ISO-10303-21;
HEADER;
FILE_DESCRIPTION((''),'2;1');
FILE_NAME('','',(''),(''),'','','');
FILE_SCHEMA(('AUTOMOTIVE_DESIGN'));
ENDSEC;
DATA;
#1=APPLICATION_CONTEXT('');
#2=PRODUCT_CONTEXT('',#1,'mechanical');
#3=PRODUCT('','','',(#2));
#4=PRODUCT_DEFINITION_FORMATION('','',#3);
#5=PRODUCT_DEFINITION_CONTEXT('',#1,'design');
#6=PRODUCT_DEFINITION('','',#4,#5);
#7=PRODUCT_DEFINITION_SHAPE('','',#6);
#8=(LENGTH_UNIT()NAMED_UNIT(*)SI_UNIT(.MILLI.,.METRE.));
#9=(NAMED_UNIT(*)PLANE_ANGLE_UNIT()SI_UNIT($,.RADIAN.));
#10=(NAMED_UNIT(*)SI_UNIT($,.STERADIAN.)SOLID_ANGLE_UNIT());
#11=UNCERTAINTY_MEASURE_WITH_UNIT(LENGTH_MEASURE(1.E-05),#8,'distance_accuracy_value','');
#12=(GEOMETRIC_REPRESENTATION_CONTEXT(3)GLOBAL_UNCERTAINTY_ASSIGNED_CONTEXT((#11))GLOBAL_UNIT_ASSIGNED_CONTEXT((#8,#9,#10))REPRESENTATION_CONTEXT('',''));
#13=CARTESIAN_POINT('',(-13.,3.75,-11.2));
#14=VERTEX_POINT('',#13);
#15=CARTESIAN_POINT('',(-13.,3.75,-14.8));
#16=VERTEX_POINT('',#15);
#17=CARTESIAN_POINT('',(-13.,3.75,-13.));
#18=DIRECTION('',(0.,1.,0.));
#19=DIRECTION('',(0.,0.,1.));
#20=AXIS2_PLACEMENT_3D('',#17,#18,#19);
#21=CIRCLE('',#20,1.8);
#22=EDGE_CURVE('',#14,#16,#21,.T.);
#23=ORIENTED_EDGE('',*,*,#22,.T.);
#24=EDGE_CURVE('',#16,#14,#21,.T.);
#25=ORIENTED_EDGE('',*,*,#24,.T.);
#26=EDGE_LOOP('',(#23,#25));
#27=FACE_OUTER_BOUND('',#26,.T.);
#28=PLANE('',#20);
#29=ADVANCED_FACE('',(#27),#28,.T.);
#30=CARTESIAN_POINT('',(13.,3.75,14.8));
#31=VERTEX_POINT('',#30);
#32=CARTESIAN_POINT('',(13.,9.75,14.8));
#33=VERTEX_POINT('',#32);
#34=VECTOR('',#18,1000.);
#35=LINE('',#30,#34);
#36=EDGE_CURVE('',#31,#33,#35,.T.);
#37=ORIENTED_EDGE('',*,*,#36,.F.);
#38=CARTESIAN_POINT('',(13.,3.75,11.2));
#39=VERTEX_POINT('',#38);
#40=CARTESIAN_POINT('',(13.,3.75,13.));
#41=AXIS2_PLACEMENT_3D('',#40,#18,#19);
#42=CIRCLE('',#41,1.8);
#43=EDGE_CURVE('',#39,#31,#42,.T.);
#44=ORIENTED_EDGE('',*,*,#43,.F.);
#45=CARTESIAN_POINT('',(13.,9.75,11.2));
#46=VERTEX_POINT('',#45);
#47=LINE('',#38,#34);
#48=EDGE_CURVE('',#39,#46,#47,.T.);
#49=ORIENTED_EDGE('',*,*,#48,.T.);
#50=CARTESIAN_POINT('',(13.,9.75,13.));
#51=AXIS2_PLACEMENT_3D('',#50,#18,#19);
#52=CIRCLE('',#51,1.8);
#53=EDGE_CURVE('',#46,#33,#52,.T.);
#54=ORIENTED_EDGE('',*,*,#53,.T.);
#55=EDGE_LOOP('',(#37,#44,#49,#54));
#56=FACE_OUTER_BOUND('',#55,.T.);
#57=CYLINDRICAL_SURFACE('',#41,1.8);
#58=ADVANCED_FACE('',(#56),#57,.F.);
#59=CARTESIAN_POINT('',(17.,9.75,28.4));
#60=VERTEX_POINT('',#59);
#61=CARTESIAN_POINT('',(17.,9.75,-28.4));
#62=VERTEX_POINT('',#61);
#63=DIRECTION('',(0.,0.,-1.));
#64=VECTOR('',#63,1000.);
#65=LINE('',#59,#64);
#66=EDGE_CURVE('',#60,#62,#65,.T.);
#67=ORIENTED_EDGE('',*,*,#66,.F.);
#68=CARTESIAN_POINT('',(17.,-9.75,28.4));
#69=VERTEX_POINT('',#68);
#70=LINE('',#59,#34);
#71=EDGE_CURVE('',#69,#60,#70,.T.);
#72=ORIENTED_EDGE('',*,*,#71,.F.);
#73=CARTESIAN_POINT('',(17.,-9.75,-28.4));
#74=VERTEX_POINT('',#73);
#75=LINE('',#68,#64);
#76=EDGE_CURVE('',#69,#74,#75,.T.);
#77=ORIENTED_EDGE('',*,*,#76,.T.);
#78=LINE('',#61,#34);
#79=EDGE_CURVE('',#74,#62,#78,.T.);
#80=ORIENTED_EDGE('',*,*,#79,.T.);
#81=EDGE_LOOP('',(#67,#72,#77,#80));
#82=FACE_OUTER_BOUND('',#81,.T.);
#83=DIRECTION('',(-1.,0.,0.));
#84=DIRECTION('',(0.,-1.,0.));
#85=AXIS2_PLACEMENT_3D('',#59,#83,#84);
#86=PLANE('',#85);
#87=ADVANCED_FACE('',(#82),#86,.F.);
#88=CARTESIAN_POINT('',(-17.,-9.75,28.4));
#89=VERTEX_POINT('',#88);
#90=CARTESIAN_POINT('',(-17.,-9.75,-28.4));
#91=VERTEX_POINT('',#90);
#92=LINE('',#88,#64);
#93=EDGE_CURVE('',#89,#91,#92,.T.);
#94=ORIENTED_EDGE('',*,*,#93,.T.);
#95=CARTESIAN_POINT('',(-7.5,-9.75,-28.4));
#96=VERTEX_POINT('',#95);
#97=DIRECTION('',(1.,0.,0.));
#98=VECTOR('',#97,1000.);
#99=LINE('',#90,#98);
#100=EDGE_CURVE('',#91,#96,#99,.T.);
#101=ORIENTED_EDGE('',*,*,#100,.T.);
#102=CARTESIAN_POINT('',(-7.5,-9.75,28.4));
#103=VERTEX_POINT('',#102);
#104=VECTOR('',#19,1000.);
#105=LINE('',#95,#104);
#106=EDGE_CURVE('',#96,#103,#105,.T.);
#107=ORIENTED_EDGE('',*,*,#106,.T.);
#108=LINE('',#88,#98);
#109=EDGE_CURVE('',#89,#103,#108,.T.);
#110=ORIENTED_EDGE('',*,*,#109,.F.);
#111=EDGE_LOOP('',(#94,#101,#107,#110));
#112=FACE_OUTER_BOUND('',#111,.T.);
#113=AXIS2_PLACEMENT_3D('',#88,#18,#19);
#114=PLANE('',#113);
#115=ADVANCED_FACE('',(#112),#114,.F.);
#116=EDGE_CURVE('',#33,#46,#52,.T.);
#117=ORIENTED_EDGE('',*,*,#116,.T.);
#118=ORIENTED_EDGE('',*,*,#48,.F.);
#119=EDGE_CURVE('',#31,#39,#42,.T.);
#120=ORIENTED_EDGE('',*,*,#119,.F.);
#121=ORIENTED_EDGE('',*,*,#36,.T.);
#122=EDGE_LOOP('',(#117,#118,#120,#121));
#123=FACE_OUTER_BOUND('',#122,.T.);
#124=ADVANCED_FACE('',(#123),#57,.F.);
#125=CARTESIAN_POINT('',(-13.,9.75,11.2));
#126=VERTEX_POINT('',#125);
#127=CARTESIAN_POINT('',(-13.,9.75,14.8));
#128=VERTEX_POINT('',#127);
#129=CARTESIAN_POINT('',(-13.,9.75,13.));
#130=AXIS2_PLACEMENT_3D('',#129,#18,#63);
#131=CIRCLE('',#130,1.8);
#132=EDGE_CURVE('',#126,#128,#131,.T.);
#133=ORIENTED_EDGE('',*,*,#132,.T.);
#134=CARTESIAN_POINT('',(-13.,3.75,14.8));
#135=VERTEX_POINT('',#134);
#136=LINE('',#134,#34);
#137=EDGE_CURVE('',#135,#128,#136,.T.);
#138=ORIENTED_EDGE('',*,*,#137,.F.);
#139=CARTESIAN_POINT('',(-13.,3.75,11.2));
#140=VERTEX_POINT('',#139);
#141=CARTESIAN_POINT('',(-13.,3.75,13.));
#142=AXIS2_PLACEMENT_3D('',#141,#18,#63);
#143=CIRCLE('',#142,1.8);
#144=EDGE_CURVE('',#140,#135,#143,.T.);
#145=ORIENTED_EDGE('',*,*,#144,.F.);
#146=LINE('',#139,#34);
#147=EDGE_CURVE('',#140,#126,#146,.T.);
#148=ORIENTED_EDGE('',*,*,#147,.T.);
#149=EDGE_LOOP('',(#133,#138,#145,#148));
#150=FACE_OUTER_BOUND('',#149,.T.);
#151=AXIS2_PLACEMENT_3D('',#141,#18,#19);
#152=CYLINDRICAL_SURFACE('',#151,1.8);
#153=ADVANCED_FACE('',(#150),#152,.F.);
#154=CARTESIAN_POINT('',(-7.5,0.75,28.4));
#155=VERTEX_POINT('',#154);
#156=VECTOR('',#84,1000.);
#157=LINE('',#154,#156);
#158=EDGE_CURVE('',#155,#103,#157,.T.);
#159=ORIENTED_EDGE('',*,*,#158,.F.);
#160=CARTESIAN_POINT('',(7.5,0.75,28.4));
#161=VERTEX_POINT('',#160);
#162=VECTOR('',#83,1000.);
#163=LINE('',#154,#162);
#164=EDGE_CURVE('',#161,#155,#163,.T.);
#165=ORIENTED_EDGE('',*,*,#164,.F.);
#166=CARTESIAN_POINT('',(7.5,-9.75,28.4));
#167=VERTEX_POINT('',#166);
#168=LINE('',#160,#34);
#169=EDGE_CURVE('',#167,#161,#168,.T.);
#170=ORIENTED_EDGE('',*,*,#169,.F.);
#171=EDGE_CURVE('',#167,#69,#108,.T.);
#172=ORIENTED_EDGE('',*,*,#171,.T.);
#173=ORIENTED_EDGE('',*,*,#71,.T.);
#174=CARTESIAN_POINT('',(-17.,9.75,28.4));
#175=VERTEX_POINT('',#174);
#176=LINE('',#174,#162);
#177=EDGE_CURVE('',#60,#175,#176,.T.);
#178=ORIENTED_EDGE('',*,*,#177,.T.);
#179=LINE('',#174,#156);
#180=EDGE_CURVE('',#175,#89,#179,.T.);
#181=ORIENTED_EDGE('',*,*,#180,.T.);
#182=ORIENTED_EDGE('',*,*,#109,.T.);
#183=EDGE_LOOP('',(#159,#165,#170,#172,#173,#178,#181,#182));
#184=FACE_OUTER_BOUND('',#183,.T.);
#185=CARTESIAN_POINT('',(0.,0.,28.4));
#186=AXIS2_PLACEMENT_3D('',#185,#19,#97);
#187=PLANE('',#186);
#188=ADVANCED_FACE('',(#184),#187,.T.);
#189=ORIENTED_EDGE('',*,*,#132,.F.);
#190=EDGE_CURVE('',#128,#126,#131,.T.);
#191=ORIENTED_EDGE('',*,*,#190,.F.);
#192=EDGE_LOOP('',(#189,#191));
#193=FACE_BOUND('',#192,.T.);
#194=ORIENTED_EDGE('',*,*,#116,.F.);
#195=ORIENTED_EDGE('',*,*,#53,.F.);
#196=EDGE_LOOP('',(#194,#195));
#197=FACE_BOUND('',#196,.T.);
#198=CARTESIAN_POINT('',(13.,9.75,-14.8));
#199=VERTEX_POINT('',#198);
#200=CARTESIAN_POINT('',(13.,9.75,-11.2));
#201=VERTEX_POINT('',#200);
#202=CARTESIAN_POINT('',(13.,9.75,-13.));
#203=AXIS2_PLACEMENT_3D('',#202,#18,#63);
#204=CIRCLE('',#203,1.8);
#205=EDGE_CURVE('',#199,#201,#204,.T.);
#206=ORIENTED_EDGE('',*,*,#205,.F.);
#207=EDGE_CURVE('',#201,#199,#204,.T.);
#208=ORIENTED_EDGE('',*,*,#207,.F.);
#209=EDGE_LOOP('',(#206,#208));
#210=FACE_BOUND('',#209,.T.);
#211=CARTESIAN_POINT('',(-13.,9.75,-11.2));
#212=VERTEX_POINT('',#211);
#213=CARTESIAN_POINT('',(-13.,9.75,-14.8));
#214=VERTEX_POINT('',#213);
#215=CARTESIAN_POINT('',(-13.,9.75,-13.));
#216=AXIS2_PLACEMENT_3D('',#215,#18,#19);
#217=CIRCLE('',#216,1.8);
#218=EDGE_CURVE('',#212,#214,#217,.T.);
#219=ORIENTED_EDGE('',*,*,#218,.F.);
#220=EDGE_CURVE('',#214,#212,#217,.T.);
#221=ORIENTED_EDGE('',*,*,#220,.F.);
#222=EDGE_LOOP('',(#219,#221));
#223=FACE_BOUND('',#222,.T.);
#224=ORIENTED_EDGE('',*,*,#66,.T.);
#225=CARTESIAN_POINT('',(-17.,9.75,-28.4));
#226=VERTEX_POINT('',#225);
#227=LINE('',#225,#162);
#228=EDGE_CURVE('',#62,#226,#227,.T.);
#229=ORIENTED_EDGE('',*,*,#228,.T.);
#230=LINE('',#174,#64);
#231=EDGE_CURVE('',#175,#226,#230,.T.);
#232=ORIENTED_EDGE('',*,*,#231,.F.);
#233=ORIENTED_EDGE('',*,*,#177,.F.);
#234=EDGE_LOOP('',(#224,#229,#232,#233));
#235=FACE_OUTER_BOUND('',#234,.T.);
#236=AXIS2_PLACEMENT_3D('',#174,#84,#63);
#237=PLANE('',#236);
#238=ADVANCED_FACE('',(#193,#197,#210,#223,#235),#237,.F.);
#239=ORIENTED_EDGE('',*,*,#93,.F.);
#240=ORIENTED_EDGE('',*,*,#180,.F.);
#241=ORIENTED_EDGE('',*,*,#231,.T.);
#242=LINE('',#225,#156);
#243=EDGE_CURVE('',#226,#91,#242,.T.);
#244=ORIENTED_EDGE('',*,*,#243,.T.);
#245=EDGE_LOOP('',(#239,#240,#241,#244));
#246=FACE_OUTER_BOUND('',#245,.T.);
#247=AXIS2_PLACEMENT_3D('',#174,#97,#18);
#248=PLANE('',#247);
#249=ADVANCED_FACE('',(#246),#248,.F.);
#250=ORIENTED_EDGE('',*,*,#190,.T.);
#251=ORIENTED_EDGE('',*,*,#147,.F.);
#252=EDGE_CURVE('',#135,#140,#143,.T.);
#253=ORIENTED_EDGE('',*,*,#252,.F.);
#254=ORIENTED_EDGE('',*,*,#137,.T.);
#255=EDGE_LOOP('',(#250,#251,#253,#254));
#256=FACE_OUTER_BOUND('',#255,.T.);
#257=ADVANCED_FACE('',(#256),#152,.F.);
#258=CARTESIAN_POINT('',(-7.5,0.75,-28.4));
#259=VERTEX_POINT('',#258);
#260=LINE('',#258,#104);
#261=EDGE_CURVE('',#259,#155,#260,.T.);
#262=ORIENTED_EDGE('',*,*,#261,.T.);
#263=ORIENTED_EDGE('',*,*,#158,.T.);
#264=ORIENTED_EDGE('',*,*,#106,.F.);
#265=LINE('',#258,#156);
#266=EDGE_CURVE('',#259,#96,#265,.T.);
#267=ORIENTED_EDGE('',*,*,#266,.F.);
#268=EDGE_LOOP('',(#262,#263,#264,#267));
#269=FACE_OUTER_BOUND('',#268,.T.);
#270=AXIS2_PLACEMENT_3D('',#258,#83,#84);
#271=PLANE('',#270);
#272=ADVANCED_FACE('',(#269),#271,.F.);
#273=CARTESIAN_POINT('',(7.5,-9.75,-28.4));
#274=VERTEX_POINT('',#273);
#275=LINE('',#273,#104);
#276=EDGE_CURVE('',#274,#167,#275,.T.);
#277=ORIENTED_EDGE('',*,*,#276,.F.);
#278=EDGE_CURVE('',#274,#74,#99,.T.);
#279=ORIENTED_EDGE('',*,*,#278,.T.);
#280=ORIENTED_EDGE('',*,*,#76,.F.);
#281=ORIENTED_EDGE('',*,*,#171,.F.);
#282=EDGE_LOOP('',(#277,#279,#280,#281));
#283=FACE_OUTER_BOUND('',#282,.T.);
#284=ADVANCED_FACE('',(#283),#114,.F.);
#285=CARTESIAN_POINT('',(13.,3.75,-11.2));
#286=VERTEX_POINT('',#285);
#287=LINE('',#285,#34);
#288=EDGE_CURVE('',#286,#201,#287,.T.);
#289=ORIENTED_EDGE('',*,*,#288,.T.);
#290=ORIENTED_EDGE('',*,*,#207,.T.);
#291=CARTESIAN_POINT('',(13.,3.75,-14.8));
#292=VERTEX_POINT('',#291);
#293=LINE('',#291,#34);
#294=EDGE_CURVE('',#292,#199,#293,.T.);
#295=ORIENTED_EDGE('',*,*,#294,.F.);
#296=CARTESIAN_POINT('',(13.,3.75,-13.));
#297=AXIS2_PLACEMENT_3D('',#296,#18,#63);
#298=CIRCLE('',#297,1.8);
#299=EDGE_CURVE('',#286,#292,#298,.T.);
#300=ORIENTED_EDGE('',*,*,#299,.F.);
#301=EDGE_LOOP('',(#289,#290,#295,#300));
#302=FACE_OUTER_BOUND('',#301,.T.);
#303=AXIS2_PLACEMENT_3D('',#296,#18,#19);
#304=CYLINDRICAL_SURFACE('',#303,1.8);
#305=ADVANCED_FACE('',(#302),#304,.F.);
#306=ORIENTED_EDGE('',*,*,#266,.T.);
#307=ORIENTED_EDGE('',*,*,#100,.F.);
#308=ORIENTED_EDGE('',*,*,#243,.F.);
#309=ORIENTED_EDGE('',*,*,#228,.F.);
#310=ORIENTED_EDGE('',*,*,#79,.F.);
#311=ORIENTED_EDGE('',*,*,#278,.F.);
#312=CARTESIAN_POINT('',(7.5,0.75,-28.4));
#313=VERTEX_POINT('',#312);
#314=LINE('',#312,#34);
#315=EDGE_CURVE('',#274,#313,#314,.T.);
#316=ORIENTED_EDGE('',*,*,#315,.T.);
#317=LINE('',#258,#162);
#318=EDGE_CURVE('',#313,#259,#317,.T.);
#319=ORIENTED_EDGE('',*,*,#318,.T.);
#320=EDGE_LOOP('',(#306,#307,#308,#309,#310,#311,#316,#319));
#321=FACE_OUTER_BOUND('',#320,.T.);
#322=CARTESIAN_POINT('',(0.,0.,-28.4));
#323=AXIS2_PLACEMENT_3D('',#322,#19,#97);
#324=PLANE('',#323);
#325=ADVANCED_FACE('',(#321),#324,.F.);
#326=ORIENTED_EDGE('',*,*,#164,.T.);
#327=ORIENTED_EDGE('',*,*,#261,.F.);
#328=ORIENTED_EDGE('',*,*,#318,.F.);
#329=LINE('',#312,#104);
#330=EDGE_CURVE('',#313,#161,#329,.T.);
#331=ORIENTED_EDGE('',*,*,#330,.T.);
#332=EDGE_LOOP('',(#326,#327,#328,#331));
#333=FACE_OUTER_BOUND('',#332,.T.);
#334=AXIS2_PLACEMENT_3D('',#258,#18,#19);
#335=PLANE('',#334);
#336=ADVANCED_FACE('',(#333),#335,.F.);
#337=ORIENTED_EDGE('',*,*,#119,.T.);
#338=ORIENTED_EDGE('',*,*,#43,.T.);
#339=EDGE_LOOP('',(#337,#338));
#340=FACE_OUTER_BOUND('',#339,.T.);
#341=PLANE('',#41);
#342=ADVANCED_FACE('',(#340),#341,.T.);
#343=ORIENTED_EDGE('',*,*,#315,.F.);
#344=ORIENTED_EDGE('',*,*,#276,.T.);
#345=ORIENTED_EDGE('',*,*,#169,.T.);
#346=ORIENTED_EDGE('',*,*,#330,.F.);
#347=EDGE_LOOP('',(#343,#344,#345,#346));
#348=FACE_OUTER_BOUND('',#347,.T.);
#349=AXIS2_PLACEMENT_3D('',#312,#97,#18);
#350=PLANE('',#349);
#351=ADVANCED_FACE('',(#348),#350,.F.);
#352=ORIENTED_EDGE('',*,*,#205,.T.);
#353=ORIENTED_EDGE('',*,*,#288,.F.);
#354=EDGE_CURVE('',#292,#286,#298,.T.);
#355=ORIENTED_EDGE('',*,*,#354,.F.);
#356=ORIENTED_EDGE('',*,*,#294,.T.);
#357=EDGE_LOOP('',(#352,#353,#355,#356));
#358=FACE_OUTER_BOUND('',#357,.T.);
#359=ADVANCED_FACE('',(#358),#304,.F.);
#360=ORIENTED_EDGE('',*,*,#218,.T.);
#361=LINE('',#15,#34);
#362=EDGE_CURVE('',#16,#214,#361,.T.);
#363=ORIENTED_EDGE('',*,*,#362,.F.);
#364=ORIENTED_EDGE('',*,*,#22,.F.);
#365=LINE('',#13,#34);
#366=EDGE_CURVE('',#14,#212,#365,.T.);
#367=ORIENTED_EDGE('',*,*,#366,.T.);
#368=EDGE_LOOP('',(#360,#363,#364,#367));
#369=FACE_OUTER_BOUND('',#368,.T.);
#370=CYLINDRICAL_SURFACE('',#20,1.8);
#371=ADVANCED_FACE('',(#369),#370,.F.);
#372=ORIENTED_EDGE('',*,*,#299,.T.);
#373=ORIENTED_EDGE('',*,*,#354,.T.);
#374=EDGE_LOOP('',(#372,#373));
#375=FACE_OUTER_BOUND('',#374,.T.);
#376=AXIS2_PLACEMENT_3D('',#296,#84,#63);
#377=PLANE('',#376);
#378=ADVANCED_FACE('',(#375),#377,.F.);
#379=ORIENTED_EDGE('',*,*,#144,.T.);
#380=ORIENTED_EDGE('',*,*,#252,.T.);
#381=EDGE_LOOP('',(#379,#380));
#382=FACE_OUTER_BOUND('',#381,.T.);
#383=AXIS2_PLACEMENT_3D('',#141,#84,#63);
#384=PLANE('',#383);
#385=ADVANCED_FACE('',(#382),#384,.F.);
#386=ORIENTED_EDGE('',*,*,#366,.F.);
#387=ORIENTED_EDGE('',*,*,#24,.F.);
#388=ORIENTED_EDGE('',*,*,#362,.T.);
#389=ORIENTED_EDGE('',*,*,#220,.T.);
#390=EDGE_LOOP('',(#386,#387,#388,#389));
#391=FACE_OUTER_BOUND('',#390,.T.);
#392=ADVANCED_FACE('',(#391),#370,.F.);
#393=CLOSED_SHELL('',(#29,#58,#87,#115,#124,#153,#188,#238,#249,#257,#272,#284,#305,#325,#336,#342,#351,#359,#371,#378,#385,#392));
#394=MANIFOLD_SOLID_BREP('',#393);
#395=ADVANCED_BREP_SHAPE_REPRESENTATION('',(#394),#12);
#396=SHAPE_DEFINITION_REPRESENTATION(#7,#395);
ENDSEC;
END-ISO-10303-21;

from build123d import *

# Parameters (mm, degrees)
SKETCH_1_W               = 34
SKETCH_1_H               = 19.5
EXTRUDE_1_DEPTH          = 28.4
CUT_EXTRUDE_1_DEPTH      = 35.505398128
CUT_EXTRUDE_1_DEPTH_BACK = 35.505398128
SKETCH_2_W               = 15
SKETCH_2_H               = 10.5
SKETCH_4_R               = 1.8
CUT_EXTRUDE_2_DEPTH      = 6


with BuildPart() as part:
    # 草图1 → 凸台-拉伸1 (new, symmetric)
    with BuildSketch(Plane.XY):
        Rectangle(SKETCH_1_W, SKETCH_1_H)
    extrude(amount=EXTRUDE_1_DEPTH, both=True)

    # 草图2 → 切除-拉伸1 (cut, two sides: drawn at the far end of the back side and taken through both)
    with BuildSketch(Plane.XY.offset(-CUT_EXTRUDE_1_DEPTH_BACK)):
        with Locations((0, -4.5)):
            Rectangle(SKETCH_2_W, SKETCH_2_H)
    extrude(amount=CUT_EXTRUDE_1_DEPTH + CUT_EXTRUDE_1_DEPTH_BACK, mode=Mode.SUBTRACT)

    # 草图4 → 切除-拉伸2 (cut)
    with BuildSketch(Plane(origin=(0, 9.75, 0), x_dir=(1, 0, 0), z_dir=(0, 1, 0))):
        with Locations(Location((-13, 13, 0), (0, 0, 270))):
            Circle(SKETCH_4_R)
        with Locations(Location((13, 13, 0), (0, 0, 90))):
            Circle(SKETCH_4_R)
        with Locations(Location((13, -13, 0), (0, 0, 270))):
            Circle(SKETCH_4_R)
        with Locations(Location((-13, -13, 0), (0, 0, 90))):
            Circle(SKETCH_4_R)
    extrude(amount=-CUT_EXTRUDE_2_DEPTH, mode=Mode.SUBTRACT)


solid = part.part
